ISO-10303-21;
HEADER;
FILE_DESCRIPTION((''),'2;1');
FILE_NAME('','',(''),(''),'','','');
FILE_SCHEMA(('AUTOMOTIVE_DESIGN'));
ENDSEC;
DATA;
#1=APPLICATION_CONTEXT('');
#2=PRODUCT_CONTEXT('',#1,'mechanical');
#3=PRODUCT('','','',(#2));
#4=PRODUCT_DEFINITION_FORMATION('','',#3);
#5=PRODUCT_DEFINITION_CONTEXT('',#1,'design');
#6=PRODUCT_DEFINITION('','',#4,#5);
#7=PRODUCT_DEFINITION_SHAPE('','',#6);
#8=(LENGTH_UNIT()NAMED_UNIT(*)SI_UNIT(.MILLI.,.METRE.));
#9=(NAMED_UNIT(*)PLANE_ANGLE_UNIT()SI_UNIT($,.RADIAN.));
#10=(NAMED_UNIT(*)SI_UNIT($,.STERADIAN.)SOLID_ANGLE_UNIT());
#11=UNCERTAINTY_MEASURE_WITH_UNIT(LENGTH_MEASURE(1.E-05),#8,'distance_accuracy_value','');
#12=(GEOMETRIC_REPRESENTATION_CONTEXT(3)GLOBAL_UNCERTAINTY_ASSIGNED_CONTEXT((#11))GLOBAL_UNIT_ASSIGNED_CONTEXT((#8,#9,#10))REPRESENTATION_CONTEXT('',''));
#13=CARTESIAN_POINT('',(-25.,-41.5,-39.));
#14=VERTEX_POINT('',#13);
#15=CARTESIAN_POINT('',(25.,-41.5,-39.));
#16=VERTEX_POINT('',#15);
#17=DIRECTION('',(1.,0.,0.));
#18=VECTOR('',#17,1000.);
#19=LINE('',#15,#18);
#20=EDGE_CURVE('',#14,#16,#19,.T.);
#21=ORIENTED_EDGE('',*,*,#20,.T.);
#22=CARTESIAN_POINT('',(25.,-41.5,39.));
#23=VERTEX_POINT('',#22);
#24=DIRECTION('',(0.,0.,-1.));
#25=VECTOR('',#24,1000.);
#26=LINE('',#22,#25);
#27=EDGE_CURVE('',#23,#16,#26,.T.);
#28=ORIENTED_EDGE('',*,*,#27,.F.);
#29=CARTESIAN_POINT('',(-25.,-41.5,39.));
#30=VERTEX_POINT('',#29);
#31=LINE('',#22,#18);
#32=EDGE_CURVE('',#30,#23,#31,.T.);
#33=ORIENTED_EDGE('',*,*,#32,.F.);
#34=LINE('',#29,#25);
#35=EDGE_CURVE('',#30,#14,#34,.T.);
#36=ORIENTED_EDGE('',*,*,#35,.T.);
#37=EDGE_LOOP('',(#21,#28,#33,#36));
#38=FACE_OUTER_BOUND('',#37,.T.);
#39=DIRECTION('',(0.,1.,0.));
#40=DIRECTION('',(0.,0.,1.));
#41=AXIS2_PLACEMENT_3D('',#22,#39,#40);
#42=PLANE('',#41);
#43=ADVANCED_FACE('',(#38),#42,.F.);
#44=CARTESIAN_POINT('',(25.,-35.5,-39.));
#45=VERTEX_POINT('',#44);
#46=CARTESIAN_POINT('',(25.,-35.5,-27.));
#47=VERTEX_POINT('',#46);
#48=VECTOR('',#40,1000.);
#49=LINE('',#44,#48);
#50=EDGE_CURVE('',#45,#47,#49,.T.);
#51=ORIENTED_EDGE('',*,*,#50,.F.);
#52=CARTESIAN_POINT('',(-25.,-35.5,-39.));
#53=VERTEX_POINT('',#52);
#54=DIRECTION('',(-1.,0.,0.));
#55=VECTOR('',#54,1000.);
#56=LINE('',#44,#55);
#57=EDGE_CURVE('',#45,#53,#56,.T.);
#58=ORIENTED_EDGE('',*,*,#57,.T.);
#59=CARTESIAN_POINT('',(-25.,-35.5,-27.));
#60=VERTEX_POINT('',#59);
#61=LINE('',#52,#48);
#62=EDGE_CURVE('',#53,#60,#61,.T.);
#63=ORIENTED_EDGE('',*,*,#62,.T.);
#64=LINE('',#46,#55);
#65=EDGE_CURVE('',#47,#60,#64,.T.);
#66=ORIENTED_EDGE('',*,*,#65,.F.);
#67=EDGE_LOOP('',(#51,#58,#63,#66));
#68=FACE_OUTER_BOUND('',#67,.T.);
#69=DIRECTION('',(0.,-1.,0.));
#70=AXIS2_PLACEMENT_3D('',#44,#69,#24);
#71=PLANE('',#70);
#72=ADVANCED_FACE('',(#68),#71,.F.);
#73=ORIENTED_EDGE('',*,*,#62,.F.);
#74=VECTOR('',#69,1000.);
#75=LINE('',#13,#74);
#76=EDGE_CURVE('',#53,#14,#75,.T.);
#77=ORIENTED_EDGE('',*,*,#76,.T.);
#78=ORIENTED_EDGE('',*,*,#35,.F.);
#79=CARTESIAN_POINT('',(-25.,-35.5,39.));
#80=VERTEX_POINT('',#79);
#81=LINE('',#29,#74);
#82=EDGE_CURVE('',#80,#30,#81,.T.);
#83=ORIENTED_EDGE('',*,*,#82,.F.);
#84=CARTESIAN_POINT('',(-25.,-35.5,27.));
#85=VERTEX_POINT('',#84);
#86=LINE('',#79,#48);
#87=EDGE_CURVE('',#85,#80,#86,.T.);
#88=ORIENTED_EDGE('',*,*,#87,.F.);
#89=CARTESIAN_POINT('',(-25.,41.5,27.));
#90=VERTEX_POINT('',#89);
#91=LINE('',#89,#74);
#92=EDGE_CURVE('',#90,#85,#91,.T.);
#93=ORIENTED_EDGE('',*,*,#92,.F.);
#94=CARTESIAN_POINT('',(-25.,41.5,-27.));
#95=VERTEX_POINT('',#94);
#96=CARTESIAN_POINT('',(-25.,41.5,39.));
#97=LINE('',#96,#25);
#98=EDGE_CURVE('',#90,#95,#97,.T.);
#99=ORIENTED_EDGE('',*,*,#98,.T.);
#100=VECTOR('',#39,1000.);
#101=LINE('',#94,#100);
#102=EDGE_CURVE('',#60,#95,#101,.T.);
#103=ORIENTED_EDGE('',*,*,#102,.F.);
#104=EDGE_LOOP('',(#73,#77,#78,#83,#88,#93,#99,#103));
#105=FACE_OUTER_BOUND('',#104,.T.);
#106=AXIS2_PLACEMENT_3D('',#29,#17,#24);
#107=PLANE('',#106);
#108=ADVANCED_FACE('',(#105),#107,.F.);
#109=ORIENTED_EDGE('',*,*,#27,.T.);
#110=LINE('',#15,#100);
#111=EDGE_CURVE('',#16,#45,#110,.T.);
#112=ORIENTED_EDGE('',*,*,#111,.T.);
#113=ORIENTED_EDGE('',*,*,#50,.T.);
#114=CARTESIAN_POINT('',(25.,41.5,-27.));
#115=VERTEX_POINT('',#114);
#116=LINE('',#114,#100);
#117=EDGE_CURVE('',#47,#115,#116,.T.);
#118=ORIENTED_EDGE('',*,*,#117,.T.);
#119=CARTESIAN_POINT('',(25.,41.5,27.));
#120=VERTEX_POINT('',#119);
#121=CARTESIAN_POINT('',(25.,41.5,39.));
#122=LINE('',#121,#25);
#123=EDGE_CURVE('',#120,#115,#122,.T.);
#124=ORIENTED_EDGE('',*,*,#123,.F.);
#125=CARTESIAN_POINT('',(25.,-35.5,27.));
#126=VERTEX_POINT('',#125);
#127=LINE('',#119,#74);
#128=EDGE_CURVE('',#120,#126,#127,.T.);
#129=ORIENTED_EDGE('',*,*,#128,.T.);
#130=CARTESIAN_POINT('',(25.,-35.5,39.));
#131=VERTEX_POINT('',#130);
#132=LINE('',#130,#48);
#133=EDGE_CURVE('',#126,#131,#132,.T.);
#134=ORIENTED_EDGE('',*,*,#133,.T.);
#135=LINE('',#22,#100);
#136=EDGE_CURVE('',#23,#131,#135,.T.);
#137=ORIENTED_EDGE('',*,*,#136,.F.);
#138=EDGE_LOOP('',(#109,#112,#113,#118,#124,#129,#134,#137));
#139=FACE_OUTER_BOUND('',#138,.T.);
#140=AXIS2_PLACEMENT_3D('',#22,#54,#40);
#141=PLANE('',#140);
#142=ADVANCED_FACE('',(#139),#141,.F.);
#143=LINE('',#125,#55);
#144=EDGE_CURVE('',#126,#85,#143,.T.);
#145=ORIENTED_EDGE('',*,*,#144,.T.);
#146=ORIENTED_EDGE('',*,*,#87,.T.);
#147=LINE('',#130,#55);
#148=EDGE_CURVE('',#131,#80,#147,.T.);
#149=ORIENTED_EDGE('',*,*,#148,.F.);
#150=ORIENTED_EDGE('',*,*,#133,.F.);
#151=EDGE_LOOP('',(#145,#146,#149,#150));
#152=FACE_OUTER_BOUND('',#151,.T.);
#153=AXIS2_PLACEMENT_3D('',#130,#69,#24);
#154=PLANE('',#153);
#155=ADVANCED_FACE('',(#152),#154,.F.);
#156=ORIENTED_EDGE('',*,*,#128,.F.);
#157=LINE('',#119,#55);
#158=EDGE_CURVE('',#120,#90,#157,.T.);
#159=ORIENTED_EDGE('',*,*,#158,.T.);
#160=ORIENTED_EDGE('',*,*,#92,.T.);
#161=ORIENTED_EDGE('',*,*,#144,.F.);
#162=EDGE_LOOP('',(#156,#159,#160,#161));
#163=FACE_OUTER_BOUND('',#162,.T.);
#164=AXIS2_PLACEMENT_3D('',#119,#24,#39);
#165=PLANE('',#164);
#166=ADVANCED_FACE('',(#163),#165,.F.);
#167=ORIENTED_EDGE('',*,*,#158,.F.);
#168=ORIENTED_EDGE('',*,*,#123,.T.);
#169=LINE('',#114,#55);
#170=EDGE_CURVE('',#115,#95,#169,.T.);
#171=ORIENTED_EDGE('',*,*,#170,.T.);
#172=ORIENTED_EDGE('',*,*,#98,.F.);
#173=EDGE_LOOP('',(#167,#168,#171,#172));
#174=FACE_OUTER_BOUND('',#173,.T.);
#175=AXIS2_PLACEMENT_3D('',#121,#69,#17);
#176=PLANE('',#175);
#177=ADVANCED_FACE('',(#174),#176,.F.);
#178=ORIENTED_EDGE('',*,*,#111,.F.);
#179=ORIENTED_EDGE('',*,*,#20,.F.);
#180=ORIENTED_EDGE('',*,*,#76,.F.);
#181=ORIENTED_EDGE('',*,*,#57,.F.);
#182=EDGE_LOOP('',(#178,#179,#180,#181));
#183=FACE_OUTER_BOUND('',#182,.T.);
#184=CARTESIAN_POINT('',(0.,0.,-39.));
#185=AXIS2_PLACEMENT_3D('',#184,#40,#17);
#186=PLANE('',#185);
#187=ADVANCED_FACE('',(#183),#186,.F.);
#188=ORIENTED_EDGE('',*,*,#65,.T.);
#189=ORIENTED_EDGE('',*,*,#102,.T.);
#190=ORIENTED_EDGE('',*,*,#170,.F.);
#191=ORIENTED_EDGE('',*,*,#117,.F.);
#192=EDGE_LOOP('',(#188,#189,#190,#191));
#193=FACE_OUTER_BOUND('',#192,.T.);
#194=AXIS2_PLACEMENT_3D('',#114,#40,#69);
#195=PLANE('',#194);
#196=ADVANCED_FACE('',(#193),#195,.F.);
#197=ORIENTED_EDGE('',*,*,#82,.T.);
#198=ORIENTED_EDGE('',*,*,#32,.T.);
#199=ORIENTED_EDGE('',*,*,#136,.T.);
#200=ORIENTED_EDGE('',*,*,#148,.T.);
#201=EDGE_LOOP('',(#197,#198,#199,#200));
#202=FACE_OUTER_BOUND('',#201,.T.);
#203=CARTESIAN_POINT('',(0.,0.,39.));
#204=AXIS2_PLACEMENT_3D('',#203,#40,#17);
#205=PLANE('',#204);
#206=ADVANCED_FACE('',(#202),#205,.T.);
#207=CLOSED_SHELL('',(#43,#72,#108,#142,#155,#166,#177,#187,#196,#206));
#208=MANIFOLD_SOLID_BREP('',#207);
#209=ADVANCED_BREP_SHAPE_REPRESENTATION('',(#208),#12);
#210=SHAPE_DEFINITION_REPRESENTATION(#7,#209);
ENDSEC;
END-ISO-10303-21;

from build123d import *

# Parameters (mm, degrees)
SKETCH1_W           = 50
SKETCH1_H           = 83
BOSS_EXTRUDE1_DEPTH = 39
SKETCH2_W           = 12
SKETCH2_H           = 77
CUT_EXTRUDE1_DEPTH  = 76.784233189


with BuildPart() as part:
    # Sketch1 → Boss-Extrude1 (new, symmetric)
    with BuildSketch(Plane.XY):
        Rectangle(SKETCH1_W, SKETCH1_H)
    extrude(amount=BOSS_EXTRUDE1_DEPTH, both=True)

    # Sketch2 → Cut-Extrude1 (cut, through all)
    with BuildSketch(Plane.ZY.offset(25)):
        with Locations((-33, 3)):
            Rectangle(SKETCH2_W, SKETCH2_H)
        with Locations((33, 3)):
            Rectangle(SKETCH2_W, SKETCH2_H)
    extrude(amount=-CUT_EXTRUDE1_DEPTH, mode=Mode.SUBTRACT)


solid = part.part
